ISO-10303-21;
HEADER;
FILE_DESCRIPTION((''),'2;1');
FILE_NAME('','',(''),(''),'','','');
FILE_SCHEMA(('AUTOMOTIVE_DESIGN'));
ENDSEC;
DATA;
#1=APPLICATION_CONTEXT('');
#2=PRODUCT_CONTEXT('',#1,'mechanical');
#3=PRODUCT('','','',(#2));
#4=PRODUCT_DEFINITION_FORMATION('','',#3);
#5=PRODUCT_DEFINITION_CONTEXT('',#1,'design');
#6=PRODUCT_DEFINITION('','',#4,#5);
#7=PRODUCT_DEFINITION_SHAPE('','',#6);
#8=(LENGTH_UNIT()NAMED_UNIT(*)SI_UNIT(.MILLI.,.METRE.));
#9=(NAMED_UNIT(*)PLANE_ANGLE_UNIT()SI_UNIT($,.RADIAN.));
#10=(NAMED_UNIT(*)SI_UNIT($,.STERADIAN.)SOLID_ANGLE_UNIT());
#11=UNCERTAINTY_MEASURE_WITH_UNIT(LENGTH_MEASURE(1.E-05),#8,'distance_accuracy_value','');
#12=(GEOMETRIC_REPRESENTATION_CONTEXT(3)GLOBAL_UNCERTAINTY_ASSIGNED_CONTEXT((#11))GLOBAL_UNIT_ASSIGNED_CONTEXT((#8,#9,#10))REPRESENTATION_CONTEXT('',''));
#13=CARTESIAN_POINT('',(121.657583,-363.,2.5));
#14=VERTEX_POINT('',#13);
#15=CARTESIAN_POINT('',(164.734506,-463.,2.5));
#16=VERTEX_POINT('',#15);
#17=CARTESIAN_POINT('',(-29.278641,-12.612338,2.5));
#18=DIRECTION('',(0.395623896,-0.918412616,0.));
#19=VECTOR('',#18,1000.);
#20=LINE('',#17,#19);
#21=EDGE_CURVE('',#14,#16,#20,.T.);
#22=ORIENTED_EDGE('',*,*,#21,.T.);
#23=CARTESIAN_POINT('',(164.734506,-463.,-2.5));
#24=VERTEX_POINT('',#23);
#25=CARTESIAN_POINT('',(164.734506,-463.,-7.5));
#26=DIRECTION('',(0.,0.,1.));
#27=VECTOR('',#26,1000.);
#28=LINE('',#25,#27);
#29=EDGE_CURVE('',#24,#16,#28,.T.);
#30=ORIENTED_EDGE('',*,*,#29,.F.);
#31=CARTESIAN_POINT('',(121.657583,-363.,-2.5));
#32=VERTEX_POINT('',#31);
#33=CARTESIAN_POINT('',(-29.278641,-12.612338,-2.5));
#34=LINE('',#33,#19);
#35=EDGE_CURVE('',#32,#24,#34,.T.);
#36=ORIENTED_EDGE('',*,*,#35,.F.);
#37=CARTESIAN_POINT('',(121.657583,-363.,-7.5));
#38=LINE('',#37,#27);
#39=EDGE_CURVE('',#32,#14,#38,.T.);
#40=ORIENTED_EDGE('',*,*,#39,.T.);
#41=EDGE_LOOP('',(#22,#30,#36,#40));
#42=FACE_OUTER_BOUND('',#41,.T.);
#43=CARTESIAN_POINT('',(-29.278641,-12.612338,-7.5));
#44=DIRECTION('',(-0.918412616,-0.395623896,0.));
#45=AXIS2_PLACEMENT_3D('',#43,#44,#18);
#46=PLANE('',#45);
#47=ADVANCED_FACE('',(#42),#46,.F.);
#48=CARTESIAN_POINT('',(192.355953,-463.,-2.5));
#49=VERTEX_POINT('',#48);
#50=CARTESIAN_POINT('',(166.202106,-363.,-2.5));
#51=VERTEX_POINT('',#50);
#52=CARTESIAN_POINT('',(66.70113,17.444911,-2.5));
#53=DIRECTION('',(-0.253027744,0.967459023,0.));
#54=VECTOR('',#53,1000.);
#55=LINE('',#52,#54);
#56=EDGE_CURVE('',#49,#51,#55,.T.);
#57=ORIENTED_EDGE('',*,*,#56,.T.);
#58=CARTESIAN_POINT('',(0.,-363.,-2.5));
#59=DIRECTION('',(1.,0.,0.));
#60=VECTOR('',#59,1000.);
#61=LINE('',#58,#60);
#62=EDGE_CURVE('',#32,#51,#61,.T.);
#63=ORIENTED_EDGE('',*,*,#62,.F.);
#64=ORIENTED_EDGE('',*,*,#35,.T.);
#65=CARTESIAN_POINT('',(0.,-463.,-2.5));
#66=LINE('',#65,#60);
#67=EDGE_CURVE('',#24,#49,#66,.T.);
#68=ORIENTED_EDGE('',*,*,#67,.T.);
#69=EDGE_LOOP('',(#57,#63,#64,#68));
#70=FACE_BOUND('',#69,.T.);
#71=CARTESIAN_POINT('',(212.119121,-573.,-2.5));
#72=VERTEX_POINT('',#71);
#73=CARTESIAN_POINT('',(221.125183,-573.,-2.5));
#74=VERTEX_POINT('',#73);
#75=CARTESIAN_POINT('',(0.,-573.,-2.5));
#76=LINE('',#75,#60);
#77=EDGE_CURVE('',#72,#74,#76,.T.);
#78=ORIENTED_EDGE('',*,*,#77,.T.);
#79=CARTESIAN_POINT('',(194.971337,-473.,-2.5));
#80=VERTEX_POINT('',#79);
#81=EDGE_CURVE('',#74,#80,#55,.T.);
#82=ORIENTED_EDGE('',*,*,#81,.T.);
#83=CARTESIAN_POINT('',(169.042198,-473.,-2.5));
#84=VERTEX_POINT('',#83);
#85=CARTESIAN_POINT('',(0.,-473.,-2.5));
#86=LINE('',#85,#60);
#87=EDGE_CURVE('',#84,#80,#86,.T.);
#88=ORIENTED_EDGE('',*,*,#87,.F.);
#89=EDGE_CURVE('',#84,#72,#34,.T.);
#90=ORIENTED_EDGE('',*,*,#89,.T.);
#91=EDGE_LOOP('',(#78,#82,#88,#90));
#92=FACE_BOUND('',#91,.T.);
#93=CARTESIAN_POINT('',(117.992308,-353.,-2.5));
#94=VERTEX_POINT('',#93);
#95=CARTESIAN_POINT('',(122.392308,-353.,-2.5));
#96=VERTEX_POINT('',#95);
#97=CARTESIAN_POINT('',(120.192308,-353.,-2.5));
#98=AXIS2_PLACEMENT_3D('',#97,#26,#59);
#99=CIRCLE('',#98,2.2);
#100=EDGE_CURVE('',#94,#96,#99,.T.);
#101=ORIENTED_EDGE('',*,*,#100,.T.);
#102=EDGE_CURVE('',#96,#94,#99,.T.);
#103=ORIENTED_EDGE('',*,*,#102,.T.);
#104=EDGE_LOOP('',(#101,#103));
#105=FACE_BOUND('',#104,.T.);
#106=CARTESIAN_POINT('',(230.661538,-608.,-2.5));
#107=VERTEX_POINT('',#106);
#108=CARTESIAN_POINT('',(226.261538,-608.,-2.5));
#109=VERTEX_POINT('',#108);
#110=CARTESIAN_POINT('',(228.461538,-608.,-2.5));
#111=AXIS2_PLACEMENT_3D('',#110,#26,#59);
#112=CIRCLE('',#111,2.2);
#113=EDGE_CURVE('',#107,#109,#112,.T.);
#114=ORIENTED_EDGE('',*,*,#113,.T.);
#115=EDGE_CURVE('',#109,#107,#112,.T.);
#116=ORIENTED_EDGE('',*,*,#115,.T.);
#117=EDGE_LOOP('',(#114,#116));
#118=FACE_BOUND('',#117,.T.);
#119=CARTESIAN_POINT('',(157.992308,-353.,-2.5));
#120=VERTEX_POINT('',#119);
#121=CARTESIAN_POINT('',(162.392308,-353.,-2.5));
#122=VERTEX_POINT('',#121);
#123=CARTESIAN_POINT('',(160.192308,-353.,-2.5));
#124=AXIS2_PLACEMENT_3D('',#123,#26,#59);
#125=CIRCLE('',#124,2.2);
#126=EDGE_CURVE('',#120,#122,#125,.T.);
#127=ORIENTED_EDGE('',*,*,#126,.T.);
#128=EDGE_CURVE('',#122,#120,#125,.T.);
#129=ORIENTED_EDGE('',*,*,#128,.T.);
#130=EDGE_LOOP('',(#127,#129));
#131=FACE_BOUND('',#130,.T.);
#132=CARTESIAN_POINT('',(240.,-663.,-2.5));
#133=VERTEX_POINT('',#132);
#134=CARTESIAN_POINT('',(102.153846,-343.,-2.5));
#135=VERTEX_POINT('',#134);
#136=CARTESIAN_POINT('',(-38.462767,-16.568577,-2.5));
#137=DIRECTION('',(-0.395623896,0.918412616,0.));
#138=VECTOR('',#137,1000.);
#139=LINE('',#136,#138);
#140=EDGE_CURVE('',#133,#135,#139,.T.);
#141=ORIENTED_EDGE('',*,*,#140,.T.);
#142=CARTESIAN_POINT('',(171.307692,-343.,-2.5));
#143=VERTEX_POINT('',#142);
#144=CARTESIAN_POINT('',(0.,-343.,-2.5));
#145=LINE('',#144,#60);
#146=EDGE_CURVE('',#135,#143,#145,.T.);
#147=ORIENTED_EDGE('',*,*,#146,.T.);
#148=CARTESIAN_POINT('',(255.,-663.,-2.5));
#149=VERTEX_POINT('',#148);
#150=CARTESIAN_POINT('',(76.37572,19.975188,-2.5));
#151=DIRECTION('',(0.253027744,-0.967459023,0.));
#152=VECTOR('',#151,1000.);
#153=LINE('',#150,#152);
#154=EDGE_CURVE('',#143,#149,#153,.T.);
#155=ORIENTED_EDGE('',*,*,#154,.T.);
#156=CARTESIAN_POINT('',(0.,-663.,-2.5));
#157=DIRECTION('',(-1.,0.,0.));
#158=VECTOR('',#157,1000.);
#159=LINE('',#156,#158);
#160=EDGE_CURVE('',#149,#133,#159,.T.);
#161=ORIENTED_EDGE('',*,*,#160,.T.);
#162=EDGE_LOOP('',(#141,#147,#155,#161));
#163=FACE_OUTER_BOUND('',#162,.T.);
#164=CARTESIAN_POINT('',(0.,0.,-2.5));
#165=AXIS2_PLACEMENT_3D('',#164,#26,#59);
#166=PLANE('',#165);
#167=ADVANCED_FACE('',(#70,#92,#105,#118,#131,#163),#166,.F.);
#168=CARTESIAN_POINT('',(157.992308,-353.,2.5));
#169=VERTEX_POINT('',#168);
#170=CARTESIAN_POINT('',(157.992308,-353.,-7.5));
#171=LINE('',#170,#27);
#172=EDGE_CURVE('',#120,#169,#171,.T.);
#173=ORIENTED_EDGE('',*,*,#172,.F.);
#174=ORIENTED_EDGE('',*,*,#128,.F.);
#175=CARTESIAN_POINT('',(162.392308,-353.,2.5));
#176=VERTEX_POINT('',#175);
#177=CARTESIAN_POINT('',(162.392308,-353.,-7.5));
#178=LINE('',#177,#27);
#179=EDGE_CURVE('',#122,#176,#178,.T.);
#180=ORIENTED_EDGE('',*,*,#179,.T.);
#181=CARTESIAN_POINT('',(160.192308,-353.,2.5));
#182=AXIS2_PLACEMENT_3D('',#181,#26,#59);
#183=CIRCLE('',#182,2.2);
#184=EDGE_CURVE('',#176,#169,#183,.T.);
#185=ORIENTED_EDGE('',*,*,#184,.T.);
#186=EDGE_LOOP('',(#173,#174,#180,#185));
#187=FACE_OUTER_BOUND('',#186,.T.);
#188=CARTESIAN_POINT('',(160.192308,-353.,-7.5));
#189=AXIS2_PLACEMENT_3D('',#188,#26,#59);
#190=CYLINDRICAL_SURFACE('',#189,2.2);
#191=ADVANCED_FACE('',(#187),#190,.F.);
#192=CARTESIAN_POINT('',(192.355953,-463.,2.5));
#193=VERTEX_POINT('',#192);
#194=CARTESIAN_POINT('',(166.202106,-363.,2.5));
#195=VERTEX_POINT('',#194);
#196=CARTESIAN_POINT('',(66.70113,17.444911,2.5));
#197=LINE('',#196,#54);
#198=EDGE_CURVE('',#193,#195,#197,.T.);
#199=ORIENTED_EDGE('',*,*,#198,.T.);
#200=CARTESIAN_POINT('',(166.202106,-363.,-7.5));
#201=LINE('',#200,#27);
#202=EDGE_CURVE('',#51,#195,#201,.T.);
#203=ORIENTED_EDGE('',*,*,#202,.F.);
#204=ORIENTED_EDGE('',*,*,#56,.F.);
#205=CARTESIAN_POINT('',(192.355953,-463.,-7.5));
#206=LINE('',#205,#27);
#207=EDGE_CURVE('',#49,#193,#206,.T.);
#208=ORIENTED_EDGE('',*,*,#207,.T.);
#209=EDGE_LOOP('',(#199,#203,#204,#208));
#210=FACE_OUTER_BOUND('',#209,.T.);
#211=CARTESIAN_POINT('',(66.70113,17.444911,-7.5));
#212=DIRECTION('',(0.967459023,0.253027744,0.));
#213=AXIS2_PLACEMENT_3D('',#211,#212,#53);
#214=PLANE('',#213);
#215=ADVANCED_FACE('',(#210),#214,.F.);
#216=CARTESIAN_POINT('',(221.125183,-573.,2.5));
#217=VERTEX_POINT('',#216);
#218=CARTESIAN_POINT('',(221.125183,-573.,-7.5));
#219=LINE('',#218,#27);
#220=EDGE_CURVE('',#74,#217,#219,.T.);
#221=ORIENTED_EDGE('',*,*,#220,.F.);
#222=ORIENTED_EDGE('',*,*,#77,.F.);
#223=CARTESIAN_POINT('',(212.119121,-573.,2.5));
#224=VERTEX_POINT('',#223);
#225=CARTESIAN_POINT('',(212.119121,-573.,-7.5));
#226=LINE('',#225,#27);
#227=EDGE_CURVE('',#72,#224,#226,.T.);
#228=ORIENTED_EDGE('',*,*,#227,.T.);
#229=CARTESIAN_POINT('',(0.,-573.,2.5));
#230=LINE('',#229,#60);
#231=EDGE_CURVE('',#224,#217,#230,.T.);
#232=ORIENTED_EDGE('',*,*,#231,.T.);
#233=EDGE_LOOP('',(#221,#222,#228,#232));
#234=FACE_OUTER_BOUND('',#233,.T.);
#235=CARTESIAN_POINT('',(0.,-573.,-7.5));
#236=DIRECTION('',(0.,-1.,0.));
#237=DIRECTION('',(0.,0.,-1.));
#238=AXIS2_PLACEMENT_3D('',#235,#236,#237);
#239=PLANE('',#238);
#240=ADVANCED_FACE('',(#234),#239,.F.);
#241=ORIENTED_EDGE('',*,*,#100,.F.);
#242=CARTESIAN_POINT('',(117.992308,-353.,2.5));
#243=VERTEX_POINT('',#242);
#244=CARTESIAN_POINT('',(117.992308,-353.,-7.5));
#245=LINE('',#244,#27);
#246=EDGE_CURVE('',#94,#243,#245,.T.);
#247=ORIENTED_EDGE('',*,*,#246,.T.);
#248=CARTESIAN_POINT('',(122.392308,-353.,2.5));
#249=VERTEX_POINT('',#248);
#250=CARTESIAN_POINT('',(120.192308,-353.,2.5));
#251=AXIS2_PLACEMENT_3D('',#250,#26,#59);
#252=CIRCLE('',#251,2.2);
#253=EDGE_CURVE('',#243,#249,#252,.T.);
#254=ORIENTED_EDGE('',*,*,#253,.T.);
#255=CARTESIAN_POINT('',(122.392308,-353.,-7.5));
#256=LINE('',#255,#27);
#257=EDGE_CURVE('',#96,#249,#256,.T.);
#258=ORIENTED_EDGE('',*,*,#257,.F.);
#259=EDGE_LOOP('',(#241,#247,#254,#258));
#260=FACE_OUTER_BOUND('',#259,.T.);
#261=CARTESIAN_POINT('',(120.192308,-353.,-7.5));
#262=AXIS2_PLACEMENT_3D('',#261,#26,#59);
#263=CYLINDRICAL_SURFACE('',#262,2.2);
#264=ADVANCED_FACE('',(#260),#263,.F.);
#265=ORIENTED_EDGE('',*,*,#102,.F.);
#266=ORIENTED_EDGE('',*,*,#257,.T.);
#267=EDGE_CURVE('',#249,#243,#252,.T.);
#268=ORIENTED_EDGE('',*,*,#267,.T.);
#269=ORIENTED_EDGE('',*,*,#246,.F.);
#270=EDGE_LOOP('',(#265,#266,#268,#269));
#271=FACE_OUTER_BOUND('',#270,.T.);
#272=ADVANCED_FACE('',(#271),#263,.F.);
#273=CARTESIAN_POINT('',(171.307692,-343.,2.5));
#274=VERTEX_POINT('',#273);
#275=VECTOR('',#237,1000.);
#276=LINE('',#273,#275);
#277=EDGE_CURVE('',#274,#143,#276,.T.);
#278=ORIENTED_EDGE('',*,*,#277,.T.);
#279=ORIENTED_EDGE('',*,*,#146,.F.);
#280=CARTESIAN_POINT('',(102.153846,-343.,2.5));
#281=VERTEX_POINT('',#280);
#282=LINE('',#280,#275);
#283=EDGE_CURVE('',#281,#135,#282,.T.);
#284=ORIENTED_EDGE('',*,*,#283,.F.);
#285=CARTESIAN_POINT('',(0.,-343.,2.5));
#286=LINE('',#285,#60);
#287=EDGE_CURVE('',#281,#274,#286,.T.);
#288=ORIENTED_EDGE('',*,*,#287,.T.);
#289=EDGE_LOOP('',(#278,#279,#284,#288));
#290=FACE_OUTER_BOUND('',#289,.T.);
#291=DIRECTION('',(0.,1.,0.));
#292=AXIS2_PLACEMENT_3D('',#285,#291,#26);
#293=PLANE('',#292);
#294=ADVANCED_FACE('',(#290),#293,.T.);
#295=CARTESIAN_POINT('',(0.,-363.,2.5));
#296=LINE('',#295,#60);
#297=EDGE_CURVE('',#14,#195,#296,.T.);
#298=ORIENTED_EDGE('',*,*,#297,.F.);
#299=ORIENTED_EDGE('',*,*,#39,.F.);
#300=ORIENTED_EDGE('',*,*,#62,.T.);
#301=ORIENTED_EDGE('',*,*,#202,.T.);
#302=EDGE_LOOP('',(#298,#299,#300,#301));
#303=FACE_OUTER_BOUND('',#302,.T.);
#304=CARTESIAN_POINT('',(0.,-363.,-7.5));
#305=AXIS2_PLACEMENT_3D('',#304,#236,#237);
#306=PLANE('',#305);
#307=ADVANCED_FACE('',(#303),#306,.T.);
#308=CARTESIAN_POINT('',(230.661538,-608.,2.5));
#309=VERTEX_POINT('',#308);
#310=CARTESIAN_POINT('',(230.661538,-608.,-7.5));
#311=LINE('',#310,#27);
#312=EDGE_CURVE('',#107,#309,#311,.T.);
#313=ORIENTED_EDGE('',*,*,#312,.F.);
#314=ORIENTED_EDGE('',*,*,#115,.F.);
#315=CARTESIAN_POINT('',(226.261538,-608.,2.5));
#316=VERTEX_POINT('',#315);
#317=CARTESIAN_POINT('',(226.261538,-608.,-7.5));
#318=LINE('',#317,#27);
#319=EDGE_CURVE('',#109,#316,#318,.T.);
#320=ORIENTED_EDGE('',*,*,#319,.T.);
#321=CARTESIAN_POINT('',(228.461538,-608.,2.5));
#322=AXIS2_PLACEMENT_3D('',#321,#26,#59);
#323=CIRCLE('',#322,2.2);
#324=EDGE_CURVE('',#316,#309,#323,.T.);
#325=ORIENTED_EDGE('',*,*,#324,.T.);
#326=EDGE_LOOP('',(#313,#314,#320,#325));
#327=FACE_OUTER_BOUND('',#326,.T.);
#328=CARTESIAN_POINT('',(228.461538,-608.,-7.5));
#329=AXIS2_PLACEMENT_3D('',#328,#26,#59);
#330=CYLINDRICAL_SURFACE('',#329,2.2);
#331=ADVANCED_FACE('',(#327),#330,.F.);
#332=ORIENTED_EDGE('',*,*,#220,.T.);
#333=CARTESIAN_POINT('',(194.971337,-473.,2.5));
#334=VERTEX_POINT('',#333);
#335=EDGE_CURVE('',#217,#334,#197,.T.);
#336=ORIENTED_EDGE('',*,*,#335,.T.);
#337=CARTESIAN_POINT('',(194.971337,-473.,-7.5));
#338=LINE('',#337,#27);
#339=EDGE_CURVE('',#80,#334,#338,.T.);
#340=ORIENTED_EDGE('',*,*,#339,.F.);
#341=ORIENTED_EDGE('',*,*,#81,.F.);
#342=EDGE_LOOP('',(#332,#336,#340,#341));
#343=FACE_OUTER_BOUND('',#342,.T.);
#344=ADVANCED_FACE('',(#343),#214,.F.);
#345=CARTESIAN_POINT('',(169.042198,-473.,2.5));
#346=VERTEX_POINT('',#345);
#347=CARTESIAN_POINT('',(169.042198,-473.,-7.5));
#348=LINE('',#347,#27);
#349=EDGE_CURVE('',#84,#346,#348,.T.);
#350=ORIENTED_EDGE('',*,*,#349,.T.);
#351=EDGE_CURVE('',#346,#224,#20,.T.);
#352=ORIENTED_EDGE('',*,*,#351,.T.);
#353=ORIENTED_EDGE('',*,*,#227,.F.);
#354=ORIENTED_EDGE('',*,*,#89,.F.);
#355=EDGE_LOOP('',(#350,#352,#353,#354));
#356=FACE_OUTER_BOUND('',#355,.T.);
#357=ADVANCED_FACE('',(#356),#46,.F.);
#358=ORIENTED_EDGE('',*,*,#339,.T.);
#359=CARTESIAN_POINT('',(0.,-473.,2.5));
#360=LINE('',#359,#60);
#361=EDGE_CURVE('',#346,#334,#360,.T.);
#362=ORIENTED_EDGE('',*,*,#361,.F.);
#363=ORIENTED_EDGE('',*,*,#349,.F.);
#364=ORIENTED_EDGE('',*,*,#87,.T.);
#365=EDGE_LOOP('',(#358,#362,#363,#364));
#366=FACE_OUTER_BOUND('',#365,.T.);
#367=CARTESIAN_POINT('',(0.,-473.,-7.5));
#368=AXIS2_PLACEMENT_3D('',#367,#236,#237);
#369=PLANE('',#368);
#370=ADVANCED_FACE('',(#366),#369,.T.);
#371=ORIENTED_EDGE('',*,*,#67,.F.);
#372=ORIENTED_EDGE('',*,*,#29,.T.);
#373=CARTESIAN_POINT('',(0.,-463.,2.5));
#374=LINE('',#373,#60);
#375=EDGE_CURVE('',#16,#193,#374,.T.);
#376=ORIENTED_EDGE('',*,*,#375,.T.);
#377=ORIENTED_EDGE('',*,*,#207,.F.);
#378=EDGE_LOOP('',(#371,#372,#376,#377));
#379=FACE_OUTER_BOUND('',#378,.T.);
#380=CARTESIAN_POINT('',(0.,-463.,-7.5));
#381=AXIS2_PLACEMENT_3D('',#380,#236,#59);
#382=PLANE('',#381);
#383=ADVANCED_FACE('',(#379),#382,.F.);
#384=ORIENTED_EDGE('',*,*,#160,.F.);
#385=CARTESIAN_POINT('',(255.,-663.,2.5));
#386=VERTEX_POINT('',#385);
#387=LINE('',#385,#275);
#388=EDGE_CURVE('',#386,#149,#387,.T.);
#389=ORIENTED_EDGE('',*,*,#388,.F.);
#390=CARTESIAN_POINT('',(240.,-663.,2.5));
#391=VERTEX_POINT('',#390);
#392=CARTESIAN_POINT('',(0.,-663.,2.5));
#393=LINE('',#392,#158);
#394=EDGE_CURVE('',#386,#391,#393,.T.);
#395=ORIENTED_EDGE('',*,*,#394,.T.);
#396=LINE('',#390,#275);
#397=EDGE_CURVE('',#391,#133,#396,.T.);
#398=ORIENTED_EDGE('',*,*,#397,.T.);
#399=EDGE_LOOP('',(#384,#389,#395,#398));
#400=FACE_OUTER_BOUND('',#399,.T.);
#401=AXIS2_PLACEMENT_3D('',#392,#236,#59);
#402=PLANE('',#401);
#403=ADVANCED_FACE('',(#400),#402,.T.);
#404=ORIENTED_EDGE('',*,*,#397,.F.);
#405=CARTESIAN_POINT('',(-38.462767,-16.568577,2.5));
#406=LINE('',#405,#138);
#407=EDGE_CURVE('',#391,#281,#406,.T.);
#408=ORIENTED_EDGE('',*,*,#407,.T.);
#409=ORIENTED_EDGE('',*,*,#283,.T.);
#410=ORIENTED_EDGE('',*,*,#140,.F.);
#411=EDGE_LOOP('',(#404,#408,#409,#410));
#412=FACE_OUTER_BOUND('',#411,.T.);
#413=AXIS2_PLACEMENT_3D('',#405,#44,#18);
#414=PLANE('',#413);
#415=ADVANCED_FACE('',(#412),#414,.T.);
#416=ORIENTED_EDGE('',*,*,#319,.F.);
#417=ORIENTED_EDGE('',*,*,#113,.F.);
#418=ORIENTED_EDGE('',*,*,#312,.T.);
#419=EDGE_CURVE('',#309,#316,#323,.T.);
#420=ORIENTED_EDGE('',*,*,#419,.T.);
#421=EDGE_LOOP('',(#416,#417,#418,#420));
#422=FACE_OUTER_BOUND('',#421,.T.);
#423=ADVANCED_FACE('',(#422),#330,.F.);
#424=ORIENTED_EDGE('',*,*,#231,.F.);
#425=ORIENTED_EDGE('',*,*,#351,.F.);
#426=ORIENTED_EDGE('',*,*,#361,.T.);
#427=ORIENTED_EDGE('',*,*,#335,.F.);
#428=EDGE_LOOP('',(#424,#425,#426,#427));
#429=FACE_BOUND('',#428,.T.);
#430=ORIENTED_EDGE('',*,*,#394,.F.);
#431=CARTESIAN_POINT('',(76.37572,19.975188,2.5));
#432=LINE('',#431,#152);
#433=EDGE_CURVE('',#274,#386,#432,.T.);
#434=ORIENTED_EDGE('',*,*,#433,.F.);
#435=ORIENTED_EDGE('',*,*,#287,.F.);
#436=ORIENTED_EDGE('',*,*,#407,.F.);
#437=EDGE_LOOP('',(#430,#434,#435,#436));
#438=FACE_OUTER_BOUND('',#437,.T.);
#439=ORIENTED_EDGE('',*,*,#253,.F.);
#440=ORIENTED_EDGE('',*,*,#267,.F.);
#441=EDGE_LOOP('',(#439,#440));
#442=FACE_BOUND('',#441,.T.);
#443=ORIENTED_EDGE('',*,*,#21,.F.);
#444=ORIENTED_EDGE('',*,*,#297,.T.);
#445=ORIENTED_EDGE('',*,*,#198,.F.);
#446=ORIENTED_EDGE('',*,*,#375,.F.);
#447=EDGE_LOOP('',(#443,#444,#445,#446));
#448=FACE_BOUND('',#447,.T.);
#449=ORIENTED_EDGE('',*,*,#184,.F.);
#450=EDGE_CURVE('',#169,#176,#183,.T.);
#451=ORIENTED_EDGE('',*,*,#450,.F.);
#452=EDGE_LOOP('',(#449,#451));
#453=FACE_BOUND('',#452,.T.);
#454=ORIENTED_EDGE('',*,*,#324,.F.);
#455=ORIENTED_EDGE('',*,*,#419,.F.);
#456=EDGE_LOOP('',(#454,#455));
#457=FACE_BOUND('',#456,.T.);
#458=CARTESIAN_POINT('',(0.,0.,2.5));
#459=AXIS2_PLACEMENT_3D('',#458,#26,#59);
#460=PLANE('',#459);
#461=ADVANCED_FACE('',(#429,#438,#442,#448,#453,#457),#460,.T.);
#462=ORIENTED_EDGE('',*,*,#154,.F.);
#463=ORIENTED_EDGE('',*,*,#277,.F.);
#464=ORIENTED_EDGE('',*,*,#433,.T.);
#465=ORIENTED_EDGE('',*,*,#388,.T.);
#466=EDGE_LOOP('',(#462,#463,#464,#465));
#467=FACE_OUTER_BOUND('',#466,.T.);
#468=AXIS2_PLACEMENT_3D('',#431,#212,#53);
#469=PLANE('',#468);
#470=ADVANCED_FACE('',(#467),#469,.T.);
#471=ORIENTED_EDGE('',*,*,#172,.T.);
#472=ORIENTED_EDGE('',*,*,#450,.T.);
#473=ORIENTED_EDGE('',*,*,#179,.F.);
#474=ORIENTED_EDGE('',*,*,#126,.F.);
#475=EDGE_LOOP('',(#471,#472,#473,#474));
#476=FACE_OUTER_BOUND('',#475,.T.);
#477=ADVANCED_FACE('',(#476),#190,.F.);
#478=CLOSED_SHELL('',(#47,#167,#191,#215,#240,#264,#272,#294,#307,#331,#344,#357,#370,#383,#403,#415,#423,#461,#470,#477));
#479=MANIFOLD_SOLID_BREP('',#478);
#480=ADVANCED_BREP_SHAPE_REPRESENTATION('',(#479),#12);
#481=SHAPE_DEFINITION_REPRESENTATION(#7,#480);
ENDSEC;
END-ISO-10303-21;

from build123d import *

# Parameters (mm, degrees)
EXTRUDE_1_DEPTH     = 2.5
SKETCH_3_R          = 2.2
CUT_EXTRUDE_1_DEPTH = 10
CUT_EXTRUDE_2_DEPTH = 10
SKETCH_5_R          = 2.2
CUT_EXTRUDE_3_DEPTH = 10


with BuildPart() as part:
    # 草图1 → 凸台-拉伸1 (new, symmetric)
    with BuildSketch(Plane.XY):
        Polygon((255, -663), (171.307692308, -343), (102.153846154, -343), (240, -663), align=None)
    extrude(amount=EXTRUDE_1_DEPTH, both=True)

    # 草图3 → 切除-拉伸1 (cut)
    with BuildSketch(Plane.XY.offset(2.5)):
        with Locations((120.192307692, -353)):
            Circle(SKETCH_3_R)
        with Locations((160.192307692, -353)):
            Circle(SKETCH_3_R)
    extrude(amount=-CUT_EXTRUDE_1_DEPTH, mode=Mode.SUBTRACT)

    # 草图4 → 切除-拉伸2 (cut)
    with BuildSketch(Plane.XY.offset(2.5)):
        Polygon((166.202106442, -363), (121.657582941, -363), (164.734506018, -463), (192.355952596, -463), align=None)
        Polygon((194.971337211, -473), (169.042198326, -473), (212.119121403, -573), (221.125183365, -573), align=None)
    extrude(amount=-CUT_EXTRUDE_2_DEPTH, mode=Mode.SUBTRACT)

    # 草图5 → 切除-拉伸3 (cut)
    with BuildSketch(Plane.XY.offset(2.5)):
        with Locations((228.461538462, -608)):
            Circle(SKETCH_5_R)
    extrude(amount=-CUT_EXTRUDE_3_DEPTH, mode=Mode.SUBTRACT)


solid = part.part
